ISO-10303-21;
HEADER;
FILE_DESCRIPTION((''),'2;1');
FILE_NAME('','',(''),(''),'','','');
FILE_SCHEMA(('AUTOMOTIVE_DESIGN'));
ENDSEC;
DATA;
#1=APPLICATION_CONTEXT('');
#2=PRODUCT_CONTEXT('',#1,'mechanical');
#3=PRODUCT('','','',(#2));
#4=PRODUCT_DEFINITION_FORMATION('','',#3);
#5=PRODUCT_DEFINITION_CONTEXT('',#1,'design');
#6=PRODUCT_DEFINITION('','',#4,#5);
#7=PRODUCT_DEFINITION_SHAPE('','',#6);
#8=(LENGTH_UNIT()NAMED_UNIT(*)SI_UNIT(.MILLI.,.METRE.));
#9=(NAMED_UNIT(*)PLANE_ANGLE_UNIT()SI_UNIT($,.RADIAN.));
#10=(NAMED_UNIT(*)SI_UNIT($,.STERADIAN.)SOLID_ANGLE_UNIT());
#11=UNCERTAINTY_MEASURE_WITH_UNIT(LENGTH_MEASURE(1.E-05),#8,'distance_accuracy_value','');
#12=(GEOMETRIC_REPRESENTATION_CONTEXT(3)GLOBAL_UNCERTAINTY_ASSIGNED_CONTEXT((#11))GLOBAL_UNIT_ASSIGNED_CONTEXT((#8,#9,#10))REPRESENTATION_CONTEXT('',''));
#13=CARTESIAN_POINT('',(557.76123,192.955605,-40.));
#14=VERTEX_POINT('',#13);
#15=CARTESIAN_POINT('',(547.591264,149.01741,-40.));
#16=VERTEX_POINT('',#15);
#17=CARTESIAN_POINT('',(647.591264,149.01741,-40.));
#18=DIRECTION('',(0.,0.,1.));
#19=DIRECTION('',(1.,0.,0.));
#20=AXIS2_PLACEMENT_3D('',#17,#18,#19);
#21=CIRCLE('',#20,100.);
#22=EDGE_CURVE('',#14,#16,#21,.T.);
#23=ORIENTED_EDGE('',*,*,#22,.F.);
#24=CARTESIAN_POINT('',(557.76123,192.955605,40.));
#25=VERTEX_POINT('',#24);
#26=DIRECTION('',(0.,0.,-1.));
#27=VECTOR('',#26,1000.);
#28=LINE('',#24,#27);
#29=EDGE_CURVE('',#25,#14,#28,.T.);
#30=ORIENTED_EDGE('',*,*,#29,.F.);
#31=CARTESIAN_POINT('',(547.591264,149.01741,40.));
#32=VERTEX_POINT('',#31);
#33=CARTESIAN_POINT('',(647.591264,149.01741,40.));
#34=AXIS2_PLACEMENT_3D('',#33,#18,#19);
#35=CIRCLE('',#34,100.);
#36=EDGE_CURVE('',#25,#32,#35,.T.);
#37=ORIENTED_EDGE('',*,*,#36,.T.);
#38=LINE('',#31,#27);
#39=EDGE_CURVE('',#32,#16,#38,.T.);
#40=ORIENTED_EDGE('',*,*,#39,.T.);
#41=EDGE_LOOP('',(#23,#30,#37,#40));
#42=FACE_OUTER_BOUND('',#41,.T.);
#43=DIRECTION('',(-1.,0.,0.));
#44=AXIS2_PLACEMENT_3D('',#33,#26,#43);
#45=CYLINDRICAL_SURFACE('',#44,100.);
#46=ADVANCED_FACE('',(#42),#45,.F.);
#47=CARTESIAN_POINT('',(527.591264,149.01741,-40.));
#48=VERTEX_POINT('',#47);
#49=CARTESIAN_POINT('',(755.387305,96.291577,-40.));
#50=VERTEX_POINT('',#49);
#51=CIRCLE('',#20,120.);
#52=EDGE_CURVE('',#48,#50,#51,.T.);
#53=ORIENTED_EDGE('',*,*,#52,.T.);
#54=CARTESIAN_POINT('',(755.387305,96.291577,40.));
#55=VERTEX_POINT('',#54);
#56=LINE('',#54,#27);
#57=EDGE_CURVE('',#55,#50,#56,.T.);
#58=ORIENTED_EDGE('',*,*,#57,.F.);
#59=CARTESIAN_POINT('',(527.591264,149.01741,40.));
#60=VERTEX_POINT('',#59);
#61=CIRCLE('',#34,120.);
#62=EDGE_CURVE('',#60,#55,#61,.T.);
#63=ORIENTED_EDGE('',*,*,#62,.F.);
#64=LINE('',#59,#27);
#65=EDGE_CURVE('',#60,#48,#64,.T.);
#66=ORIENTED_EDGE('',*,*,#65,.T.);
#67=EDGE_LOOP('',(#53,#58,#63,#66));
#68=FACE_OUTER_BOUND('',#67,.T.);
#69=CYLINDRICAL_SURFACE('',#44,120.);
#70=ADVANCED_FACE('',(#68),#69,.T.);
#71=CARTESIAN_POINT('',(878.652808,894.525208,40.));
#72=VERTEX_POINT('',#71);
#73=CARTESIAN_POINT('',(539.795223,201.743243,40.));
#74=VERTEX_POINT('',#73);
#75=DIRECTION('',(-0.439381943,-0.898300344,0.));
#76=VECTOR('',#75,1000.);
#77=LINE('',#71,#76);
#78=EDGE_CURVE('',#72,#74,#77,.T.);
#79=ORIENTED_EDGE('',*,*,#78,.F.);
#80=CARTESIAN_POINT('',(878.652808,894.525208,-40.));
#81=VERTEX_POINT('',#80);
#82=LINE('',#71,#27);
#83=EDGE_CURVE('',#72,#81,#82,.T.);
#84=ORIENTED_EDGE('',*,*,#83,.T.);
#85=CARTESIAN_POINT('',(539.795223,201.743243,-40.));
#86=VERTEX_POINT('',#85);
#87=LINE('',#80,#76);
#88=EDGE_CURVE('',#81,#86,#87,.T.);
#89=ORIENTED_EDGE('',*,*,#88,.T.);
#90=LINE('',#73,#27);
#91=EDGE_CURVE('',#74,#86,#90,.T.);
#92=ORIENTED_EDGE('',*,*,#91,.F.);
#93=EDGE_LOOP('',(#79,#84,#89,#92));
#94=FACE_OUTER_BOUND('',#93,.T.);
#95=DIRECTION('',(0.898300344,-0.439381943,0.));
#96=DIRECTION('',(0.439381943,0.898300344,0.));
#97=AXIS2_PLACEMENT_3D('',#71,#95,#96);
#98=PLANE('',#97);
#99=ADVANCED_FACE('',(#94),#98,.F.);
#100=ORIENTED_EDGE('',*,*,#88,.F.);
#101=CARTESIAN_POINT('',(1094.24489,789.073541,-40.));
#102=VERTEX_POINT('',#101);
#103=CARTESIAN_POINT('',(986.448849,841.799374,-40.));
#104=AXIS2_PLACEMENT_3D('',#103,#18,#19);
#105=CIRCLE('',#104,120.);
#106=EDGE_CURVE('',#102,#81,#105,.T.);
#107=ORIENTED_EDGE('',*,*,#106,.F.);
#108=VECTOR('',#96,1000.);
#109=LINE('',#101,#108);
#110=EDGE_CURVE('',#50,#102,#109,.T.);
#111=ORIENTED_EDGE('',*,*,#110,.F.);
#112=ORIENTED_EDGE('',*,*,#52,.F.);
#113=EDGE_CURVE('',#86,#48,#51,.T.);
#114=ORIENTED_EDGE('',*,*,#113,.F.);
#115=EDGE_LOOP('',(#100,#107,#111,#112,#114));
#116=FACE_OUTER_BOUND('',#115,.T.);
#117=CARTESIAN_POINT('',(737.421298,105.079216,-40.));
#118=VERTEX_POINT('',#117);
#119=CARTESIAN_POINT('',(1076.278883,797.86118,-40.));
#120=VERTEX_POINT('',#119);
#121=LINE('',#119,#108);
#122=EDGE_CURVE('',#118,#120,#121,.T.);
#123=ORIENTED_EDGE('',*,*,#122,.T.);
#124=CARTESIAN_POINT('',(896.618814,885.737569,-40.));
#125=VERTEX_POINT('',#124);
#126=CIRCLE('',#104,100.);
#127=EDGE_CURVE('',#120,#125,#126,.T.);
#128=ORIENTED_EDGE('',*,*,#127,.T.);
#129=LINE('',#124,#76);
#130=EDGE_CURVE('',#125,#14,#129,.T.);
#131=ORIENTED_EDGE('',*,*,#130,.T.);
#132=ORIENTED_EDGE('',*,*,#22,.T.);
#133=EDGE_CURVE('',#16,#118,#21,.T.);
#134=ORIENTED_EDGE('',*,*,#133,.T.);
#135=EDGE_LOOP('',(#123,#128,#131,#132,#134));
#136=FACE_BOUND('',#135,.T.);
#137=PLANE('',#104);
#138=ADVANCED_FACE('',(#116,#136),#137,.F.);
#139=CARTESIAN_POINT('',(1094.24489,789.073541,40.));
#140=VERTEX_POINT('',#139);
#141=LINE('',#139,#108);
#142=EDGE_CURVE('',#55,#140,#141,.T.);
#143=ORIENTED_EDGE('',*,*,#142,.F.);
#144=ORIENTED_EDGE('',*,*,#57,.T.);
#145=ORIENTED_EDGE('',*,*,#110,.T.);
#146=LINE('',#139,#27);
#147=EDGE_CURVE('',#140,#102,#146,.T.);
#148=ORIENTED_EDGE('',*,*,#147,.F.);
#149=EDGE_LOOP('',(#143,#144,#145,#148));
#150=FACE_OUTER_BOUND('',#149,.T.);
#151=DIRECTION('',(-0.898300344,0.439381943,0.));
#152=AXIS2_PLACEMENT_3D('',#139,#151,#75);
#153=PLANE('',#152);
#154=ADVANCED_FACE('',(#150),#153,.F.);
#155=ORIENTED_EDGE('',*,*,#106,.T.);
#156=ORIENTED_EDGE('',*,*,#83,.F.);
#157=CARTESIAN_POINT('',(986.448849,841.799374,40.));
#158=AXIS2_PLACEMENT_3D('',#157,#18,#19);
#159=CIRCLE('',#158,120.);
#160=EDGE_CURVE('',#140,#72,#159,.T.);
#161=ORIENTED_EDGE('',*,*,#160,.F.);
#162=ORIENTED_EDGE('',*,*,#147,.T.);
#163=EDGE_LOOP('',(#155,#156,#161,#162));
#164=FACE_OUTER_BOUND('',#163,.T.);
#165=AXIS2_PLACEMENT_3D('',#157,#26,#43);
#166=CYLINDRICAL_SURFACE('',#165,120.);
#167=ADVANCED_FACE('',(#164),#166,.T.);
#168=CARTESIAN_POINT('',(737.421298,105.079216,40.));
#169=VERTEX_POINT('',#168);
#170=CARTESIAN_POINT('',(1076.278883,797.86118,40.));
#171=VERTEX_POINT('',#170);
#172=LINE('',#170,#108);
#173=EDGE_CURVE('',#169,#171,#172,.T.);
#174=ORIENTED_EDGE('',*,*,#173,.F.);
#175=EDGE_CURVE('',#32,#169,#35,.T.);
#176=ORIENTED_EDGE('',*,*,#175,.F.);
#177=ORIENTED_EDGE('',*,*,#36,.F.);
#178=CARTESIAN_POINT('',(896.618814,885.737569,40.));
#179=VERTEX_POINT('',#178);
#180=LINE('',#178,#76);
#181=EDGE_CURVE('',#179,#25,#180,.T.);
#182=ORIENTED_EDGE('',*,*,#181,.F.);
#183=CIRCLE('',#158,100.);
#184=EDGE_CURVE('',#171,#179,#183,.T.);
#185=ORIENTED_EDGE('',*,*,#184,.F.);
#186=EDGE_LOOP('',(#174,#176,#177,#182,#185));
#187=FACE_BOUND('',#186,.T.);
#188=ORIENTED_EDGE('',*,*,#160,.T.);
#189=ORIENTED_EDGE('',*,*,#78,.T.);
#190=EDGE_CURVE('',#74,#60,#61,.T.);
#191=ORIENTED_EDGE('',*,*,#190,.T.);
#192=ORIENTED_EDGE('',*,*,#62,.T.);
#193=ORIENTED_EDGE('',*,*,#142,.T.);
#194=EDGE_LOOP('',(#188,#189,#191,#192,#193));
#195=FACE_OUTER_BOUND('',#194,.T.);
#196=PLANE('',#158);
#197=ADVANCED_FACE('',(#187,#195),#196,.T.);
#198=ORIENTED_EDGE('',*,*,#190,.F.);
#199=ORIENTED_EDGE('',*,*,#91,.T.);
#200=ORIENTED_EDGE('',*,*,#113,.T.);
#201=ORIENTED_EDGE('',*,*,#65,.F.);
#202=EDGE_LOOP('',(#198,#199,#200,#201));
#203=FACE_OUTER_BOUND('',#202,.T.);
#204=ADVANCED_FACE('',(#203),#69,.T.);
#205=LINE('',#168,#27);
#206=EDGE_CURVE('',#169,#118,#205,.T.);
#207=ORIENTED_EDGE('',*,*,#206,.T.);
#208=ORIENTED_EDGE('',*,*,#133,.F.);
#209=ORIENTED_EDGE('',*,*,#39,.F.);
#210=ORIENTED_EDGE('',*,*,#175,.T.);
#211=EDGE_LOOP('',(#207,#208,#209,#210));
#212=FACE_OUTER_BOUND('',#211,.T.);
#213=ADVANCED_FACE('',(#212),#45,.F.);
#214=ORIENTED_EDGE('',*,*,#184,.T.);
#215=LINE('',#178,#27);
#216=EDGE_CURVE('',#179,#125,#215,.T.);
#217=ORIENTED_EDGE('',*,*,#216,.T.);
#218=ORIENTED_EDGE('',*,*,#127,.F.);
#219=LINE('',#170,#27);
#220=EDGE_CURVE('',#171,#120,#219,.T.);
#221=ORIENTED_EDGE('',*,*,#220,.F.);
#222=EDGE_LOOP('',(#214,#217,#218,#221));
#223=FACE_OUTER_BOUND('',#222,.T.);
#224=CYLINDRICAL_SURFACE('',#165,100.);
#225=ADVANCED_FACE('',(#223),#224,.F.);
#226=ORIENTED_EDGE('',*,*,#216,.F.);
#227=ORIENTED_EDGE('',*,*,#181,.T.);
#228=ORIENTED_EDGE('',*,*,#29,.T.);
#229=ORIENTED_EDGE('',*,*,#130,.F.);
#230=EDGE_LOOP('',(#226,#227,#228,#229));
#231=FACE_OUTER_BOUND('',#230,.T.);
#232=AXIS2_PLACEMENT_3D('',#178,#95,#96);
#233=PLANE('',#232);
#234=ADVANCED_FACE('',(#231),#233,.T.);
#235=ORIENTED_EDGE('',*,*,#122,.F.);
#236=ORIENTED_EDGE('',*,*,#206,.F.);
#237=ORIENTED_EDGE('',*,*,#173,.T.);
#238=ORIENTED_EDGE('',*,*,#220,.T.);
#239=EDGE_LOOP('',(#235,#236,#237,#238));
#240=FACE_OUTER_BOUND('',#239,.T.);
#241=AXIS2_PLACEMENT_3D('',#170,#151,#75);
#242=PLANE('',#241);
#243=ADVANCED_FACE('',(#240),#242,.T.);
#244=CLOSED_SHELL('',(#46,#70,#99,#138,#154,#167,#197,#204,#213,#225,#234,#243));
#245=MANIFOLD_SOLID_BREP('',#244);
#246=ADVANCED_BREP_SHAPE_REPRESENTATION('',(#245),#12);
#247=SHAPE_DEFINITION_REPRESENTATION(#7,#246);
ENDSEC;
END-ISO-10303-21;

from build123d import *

# Parameters (mm, degrees)
EXTRUDE_1_DEPTH = 40


with BuildPart() as part:
    # 草图1 → 凸台-拉伸1 (new, symmetric)
    with BuildSketch(Plane.XY):
        with BuildLine():
            Line((878.652807565, 894.525207523), (539.795222723, 201.743243487))
            ThreePointArc((539.795222723, 201.743243487), (594.86543093, 41.221369064), (755.387305352, 96.291577272))
            Line((755.387305352, 96.291577272), (1094.244890195, 789.073541309))
            ThreePointArc((1094.244890195, 789.073541309), (1039.174681987, 949.595415731), (878.652807565, 894.525207523))
        make_face()
        with BuildLine():
            Line((896.618814451, 885.737568672), (557.761229608, 192.955604635))
            ThreePointArc((557.761229608, 192.955604635), (603.653069781, 59.18737595), (737.421298466, 105.079216123))
            Line((737.421298466, 105.079216123), (1076.278883309, 797.86118016))
            ThreePointArc((1076.278883309, 797.86118016), (1030.387043136, 931.629408845), (896.618814451, 885.737568672))
        make_face(mode=Mode.SUBTRACT)
    extrude(amount=EXTRUDE_1_DEPTH, both=True)


solid = part.part
